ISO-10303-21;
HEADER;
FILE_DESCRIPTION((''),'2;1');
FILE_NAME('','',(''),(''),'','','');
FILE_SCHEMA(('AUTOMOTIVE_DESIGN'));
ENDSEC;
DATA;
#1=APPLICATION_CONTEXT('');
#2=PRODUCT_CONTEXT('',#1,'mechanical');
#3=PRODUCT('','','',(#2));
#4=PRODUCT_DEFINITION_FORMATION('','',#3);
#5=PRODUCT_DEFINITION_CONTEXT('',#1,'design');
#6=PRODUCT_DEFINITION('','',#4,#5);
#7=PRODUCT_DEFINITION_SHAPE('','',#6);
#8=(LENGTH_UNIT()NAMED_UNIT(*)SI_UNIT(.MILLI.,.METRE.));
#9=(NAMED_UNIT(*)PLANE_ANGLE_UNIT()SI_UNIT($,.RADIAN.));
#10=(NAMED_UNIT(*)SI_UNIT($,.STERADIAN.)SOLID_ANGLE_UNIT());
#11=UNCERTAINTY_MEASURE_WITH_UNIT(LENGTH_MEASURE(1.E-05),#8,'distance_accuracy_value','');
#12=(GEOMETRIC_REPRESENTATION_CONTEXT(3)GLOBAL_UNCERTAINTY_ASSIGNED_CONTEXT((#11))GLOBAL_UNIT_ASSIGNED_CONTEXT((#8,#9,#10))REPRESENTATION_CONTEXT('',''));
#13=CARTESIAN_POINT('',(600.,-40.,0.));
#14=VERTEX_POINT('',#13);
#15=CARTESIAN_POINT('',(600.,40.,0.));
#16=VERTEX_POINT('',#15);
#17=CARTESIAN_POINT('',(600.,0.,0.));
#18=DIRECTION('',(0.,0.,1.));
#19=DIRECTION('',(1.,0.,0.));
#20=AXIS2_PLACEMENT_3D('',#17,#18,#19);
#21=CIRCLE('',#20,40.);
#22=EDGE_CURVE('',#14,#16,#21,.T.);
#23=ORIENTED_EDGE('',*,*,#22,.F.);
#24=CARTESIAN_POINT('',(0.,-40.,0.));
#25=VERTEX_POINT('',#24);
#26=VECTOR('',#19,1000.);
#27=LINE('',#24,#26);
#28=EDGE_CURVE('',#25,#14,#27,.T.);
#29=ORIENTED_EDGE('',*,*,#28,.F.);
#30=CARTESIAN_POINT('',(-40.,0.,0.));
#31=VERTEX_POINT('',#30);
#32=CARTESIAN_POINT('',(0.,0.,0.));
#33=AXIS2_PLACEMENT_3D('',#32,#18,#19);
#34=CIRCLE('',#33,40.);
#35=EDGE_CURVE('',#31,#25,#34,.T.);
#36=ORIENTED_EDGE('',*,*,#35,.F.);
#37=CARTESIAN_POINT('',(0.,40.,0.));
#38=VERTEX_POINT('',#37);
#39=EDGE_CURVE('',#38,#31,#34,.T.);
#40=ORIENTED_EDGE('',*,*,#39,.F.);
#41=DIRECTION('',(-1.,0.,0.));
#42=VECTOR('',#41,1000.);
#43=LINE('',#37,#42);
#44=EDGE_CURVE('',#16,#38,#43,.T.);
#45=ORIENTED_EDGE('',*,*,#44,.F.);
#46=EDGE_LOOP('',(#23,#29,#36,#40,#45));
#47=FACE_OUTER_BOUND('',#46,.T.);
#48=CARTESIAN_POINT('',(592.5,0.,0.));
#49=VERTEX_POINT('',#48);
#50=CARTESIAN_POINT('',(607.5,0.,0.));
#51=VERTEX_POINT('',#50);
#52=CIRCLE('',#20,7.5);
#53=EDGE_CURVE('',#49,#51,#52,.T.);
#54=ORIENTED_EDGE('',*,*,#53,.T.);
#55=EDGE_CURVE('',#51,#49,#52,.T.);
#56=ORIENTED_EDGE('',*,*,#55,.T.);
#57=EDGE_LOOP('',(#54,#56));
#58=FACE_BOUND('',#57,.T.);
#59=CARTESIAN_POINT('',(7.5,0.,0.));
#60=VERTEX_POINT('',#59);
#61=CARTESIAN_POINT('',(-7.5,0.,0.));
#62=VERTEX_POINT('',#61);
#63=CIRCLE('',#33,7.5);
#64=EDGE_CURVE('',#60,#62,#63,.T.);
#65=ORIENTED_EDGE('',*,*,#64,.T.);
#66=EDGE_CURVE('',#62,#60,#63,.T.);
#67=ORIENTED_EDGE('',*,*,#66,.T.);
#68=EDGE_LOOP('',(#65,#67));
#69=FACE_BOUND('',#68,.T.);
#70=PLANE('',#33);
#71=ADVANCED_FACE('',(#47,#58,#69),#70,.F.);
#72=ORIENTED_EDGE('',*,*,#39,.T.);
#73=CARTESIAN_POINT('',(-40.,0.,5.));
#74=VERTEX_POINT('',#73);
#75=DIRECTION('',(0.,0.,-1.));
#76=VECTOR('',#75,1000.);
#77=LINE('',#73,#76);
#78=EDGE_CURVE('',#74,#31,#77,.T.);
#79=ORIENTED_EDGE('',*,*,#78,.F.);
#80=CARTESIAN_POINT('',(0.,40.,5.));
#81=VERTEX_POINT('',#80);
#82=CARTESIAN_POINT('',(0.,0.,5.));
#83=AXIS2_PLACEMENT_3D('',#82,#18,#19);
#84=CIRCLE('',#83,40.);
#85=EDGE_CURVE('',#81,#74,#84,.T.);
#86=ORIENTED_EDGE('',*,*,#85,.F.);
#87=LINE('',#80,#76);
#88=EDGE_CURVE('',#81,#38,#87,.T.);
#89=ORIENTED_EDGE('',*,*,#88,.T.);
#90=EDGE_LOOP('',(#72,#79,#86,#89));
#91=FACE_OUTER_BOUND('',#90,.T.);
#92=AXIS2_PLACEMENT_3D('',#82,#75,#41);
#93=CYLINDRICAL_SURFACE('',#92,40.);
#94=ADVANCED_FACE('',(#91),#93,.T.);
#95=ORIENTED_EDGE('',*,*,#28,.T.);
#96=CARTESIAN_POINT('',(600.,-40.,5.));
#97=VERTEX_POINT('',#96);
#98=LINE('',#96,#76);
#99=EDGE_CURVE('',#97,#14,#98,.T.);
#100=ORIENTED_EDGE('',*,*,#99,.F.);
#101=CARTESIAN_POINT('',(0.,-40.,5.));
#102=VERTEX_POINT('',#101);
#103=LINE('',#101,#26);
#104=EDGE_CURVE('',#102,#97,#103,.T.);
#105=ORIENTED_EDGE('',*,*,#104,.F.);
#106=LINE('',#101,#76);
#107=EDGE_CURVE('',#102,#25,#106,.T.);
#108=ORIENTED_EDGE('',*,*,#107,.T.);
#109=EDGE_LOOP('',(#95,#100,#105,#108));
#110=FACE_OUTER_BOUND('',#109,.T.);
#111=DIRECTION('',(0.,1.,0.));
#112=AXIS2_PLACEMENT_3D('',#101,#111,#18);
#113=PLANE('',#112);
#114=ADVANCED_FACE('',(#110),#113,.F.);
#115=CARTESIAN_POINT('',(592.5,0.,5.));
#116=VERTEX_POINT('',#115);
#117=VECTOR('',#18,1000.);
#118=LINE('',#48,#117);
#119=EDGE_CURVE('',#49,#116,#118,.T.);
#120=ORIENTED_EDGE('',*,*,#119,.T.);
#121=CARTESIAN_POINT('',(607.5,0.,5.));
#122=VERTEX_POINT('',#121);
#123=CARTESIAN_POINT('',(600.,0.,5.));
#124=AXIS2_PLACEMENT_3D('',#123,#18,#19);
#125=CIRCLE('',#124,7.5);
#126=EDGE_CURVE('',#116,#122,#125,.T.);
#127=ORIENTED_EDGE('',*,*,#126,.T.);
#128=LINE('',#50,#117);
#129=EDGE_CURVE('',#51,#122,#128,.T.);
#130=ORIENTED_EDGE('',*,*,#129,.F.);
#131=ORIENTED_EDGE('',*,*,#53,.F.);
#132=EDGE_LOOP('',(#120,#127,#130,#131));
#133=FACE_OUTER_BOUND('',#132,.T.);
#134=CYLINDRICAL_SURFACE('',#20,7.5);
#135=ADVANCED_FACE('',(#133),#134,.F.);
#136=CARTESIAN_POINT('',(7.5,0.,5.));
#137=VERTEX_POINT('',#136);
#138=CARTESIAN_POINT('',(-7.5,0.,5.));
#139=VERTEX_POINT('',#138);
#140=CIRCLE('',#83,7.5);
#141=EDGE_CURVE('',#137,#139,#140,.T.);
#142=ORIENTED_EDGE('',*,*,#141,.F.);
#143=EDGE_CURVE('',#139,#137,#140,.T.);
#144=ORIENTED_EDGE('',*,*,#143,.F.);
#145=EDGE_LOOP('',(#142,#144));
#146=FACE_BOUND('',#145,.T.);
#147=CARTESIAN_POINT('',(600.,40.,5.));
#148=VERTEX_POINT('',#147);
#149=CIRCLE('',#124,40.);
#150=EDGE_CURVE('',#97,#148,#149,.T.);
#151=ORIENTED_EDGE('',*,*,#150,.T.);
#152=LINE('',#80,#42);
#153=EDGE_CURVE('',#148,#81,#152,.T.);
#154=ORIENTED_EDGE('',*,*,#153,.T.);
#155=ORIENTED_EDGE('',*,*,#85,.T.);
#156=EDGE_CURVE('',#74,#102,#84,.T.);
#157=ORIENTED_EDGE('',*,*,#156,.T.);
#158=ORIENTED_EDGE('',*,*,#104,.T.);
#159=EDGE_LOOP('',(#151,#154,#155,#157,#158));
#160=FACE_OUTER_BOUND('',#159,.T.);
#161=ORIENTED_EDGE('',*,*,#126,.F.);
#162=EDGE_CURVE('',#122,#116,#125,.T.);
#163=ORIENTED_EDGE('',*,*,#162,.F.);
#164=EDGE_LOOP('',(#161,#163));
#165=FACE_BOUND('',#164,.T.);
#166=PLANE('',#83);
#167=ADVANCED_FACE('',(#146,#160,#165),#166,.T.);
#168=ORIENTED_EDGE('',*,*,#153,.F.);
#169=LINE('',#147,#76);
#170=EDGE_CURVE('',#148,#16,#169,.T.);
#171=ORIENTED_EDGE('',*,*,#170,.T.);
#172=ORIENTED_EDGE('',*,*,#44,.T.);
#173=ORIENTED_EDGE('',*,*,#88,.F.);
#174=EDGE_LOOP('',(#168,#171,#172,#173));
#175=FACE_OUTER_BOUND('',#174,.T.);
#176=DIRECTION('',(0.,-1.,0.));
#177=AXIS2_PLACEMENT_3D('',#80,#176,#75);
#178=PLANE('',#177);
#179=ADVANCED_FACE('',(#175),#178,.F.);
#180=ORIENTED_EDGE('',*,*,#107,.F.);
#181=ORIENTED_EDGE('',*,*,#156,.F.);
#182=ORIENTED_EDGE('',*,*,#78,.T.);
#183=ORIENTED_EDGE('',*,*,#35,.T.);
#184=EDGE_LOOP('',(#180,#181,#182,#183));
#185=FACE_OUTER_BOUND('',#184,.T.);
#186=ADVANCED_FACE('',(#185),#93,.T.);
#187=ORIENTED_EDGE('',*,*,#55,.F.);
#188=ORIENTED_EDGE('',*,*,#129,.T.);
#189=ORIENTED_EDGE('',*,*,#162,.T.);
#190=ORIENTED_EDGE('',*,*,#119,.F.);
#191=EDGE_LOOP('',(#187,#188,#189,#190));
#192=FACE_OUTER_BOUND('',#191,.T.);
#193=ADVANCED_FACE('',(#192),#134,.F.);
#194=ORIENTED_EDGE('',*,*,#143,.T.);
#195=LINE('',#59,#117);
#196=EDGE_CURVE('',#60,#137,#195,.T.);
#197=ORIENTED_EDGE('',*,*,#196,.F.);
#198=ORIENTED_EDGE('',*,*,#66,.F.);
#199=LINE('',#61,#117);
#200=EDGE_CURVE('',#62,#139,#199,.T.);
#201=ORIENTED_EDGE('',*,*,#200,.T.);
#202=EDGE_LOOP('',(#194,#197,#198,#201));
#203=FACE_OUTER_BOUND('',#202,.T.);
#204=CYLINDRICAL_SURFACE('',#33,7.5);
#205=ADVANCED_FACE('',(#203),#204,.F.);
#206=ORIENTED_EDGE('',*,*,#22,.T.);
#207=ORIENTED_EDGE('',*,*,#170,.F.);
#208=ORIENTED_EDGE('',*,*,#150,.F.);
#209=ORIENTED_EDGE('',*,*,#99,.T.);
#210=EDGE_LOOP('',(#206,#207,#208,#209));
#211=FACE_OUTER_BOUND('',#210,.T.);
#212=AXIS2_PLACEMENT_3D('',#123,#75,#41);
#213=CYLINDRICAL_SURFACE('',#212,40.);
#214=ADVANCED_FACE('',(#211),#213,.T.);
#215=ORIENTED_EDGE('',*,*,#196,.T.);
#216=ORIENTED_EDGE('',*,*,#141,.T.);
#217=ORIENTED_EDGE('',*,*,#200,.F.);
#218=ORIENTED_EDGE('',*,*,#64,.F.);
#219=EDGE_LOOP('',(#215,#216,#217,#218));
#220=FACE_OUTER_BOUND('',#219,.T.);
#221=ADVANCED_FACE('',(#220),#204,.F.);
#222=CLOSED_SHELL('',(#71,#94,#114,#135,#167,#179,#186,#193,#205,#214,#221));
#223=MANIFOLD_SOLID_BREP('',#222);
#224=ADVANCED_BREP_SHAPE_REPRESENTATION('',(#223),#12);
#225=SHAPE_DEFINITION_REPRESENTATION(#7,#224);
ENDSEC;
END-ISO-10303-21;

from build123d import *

# Parameters (mm, degrees)
EXTRUDE_1_DEPTH     = 5
SKETCH_2_R          = 7.5
CUT_EXTRUDE_1_DEPTH = 642.268274593


with BuildPart() as part:
    # 草图1 → 凸台-拉伸1 (new body)
    with BuildSketch(Plane.XY):
        with BuildLine():
            Line((0, 40), (600, 40))
            ThreePointArc((600, 40), (640, 0), (600, -40))
            Line((600, -40), (0, -40))
            ThreePointArc((0, -40), (-40, 0), (0, 40))
        make_face()
    extrude(amount=EXTRUDE_1_DEPTH)

    # 草图2 → 切除-拉伸1 (cut, through all)
    with BuildSketch(Plane.XY.offset(5)):
        Circle(SKETCH_2_R)
        with Locations((600, 0)):
            Circle(SKETCH_2_R)
    extrude(amount=-CUT_EXTRUDE_1_DEPTH, mode=Mode.SUBTRACT)


solid = part.part
